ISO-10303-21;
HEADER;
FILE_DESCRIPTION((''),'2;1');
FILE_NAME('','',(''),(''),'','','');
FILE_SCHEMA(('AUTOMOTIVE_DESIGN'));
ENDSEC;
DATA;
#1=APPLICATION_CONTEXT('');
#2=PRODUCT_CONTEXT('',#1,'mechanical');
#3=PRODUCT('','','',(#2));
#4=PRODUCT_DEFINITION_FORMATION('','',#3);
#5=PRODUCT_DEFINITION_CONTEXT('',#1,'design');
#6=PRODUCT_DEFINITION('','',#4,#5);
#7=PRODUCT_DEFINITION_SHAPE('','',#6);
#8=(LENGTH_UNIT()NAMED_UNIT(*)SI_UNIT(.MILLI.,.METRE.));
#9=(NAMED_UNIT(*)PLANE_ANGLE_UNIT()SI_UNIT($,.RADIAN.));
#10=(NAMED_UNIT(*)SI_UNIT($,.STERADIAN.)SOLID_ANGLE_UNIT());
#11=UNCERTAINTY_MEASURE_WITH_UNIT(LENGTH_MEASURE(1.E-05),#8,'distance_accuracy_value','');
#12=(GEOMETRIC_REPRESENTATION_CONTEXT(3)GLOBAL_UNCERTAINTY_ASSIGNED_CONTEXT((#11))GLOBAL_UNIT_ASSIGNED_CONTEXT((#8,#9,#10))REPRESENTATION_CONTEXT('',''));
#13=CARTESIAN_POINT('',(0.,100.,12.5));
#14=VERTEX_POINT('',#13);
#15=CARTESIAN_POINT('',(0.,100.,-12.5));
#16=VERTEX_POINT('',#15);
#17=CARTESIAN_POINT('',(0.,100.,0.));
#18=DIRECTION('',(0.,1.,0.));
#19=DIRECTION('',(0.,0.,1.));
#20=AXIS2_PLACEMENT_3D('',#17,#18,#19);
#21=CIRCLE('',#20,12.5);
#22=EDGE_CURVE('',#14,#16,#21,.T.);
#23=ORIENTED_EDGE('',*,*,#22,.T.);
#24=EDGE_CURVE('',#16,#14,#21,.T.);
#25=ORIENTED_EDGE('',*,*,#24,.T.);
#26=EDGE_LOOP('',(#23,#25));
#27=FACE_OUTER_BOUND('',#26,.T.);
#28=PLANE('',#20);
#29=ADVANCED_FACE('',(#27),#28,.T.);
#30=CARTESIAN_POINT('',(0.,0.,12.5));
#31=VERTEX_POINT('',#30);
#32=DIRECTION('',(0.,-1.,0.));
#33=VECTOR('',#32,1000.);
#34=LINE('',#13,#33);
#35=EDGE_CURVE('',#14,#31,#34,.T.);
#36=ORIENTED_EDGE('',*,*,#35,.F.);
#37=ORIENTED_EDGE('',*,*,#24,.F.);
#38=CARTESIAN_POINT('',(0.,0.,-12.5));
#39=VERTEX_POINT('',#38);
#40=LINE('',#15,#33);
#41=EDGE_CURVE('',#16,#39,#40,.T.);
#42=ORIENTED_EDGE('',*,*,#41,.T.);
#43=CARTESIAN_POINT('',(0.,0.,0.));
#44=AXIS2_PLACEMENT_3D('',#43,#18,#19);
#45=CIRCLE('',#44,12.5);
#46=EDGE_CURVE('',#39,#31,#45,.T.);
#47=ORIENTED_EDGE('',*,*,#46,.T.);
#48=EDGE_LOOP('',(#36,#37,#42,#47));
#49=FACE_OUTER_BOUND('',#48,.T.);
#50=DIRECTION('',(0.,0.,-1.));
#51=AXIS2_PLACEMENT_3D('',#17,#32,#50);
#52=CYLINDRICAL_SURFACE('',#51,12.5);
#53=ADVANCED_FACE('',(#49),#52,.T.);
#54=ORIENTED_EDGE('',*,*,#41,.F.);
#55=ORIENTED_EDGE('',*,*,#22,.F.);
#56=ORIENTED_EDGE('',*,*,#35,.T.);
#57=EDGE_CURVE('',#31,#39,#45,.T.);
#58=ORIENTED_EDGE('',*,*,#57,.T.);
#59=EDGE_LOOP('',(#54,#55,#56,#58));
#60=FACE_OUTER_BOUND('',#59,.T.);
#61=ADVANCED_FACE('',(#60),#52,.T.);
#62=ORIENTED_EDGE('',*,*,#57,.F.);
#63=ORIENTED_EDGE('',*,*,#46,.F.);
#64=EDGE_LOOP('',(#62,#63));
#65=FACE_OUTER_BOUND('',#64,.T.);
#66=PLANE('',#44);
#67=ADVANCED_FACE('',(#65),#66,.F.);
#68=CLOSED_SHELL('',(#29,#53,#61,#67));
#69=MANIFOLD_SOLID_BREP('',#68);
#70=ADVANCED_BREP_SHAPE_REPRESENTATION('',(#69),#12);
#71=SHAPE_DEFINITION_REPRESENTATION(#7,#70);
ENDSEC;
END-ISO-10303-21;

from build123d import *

# Parameters (mm, degrees)
SKETCH1_R           = 12.5
BOSS_EXTRUDE1_DEPTH = 100


with BuildPart() as part:
    # Sketch1 → Boss-Extrude1 (new body)
    with BuildSketch(Plane(origin=(0, 0, 0), x_dir=(1, 0, 0), z_dir=(0, 1, 0))):
        with Locations(Location((0, 0, 0), (0, 0, 90))):
            Circle(SKETCH1_R)
    extrude(amount=BOSS_EXTRUDE1_DEPTH)


solid = part.part
